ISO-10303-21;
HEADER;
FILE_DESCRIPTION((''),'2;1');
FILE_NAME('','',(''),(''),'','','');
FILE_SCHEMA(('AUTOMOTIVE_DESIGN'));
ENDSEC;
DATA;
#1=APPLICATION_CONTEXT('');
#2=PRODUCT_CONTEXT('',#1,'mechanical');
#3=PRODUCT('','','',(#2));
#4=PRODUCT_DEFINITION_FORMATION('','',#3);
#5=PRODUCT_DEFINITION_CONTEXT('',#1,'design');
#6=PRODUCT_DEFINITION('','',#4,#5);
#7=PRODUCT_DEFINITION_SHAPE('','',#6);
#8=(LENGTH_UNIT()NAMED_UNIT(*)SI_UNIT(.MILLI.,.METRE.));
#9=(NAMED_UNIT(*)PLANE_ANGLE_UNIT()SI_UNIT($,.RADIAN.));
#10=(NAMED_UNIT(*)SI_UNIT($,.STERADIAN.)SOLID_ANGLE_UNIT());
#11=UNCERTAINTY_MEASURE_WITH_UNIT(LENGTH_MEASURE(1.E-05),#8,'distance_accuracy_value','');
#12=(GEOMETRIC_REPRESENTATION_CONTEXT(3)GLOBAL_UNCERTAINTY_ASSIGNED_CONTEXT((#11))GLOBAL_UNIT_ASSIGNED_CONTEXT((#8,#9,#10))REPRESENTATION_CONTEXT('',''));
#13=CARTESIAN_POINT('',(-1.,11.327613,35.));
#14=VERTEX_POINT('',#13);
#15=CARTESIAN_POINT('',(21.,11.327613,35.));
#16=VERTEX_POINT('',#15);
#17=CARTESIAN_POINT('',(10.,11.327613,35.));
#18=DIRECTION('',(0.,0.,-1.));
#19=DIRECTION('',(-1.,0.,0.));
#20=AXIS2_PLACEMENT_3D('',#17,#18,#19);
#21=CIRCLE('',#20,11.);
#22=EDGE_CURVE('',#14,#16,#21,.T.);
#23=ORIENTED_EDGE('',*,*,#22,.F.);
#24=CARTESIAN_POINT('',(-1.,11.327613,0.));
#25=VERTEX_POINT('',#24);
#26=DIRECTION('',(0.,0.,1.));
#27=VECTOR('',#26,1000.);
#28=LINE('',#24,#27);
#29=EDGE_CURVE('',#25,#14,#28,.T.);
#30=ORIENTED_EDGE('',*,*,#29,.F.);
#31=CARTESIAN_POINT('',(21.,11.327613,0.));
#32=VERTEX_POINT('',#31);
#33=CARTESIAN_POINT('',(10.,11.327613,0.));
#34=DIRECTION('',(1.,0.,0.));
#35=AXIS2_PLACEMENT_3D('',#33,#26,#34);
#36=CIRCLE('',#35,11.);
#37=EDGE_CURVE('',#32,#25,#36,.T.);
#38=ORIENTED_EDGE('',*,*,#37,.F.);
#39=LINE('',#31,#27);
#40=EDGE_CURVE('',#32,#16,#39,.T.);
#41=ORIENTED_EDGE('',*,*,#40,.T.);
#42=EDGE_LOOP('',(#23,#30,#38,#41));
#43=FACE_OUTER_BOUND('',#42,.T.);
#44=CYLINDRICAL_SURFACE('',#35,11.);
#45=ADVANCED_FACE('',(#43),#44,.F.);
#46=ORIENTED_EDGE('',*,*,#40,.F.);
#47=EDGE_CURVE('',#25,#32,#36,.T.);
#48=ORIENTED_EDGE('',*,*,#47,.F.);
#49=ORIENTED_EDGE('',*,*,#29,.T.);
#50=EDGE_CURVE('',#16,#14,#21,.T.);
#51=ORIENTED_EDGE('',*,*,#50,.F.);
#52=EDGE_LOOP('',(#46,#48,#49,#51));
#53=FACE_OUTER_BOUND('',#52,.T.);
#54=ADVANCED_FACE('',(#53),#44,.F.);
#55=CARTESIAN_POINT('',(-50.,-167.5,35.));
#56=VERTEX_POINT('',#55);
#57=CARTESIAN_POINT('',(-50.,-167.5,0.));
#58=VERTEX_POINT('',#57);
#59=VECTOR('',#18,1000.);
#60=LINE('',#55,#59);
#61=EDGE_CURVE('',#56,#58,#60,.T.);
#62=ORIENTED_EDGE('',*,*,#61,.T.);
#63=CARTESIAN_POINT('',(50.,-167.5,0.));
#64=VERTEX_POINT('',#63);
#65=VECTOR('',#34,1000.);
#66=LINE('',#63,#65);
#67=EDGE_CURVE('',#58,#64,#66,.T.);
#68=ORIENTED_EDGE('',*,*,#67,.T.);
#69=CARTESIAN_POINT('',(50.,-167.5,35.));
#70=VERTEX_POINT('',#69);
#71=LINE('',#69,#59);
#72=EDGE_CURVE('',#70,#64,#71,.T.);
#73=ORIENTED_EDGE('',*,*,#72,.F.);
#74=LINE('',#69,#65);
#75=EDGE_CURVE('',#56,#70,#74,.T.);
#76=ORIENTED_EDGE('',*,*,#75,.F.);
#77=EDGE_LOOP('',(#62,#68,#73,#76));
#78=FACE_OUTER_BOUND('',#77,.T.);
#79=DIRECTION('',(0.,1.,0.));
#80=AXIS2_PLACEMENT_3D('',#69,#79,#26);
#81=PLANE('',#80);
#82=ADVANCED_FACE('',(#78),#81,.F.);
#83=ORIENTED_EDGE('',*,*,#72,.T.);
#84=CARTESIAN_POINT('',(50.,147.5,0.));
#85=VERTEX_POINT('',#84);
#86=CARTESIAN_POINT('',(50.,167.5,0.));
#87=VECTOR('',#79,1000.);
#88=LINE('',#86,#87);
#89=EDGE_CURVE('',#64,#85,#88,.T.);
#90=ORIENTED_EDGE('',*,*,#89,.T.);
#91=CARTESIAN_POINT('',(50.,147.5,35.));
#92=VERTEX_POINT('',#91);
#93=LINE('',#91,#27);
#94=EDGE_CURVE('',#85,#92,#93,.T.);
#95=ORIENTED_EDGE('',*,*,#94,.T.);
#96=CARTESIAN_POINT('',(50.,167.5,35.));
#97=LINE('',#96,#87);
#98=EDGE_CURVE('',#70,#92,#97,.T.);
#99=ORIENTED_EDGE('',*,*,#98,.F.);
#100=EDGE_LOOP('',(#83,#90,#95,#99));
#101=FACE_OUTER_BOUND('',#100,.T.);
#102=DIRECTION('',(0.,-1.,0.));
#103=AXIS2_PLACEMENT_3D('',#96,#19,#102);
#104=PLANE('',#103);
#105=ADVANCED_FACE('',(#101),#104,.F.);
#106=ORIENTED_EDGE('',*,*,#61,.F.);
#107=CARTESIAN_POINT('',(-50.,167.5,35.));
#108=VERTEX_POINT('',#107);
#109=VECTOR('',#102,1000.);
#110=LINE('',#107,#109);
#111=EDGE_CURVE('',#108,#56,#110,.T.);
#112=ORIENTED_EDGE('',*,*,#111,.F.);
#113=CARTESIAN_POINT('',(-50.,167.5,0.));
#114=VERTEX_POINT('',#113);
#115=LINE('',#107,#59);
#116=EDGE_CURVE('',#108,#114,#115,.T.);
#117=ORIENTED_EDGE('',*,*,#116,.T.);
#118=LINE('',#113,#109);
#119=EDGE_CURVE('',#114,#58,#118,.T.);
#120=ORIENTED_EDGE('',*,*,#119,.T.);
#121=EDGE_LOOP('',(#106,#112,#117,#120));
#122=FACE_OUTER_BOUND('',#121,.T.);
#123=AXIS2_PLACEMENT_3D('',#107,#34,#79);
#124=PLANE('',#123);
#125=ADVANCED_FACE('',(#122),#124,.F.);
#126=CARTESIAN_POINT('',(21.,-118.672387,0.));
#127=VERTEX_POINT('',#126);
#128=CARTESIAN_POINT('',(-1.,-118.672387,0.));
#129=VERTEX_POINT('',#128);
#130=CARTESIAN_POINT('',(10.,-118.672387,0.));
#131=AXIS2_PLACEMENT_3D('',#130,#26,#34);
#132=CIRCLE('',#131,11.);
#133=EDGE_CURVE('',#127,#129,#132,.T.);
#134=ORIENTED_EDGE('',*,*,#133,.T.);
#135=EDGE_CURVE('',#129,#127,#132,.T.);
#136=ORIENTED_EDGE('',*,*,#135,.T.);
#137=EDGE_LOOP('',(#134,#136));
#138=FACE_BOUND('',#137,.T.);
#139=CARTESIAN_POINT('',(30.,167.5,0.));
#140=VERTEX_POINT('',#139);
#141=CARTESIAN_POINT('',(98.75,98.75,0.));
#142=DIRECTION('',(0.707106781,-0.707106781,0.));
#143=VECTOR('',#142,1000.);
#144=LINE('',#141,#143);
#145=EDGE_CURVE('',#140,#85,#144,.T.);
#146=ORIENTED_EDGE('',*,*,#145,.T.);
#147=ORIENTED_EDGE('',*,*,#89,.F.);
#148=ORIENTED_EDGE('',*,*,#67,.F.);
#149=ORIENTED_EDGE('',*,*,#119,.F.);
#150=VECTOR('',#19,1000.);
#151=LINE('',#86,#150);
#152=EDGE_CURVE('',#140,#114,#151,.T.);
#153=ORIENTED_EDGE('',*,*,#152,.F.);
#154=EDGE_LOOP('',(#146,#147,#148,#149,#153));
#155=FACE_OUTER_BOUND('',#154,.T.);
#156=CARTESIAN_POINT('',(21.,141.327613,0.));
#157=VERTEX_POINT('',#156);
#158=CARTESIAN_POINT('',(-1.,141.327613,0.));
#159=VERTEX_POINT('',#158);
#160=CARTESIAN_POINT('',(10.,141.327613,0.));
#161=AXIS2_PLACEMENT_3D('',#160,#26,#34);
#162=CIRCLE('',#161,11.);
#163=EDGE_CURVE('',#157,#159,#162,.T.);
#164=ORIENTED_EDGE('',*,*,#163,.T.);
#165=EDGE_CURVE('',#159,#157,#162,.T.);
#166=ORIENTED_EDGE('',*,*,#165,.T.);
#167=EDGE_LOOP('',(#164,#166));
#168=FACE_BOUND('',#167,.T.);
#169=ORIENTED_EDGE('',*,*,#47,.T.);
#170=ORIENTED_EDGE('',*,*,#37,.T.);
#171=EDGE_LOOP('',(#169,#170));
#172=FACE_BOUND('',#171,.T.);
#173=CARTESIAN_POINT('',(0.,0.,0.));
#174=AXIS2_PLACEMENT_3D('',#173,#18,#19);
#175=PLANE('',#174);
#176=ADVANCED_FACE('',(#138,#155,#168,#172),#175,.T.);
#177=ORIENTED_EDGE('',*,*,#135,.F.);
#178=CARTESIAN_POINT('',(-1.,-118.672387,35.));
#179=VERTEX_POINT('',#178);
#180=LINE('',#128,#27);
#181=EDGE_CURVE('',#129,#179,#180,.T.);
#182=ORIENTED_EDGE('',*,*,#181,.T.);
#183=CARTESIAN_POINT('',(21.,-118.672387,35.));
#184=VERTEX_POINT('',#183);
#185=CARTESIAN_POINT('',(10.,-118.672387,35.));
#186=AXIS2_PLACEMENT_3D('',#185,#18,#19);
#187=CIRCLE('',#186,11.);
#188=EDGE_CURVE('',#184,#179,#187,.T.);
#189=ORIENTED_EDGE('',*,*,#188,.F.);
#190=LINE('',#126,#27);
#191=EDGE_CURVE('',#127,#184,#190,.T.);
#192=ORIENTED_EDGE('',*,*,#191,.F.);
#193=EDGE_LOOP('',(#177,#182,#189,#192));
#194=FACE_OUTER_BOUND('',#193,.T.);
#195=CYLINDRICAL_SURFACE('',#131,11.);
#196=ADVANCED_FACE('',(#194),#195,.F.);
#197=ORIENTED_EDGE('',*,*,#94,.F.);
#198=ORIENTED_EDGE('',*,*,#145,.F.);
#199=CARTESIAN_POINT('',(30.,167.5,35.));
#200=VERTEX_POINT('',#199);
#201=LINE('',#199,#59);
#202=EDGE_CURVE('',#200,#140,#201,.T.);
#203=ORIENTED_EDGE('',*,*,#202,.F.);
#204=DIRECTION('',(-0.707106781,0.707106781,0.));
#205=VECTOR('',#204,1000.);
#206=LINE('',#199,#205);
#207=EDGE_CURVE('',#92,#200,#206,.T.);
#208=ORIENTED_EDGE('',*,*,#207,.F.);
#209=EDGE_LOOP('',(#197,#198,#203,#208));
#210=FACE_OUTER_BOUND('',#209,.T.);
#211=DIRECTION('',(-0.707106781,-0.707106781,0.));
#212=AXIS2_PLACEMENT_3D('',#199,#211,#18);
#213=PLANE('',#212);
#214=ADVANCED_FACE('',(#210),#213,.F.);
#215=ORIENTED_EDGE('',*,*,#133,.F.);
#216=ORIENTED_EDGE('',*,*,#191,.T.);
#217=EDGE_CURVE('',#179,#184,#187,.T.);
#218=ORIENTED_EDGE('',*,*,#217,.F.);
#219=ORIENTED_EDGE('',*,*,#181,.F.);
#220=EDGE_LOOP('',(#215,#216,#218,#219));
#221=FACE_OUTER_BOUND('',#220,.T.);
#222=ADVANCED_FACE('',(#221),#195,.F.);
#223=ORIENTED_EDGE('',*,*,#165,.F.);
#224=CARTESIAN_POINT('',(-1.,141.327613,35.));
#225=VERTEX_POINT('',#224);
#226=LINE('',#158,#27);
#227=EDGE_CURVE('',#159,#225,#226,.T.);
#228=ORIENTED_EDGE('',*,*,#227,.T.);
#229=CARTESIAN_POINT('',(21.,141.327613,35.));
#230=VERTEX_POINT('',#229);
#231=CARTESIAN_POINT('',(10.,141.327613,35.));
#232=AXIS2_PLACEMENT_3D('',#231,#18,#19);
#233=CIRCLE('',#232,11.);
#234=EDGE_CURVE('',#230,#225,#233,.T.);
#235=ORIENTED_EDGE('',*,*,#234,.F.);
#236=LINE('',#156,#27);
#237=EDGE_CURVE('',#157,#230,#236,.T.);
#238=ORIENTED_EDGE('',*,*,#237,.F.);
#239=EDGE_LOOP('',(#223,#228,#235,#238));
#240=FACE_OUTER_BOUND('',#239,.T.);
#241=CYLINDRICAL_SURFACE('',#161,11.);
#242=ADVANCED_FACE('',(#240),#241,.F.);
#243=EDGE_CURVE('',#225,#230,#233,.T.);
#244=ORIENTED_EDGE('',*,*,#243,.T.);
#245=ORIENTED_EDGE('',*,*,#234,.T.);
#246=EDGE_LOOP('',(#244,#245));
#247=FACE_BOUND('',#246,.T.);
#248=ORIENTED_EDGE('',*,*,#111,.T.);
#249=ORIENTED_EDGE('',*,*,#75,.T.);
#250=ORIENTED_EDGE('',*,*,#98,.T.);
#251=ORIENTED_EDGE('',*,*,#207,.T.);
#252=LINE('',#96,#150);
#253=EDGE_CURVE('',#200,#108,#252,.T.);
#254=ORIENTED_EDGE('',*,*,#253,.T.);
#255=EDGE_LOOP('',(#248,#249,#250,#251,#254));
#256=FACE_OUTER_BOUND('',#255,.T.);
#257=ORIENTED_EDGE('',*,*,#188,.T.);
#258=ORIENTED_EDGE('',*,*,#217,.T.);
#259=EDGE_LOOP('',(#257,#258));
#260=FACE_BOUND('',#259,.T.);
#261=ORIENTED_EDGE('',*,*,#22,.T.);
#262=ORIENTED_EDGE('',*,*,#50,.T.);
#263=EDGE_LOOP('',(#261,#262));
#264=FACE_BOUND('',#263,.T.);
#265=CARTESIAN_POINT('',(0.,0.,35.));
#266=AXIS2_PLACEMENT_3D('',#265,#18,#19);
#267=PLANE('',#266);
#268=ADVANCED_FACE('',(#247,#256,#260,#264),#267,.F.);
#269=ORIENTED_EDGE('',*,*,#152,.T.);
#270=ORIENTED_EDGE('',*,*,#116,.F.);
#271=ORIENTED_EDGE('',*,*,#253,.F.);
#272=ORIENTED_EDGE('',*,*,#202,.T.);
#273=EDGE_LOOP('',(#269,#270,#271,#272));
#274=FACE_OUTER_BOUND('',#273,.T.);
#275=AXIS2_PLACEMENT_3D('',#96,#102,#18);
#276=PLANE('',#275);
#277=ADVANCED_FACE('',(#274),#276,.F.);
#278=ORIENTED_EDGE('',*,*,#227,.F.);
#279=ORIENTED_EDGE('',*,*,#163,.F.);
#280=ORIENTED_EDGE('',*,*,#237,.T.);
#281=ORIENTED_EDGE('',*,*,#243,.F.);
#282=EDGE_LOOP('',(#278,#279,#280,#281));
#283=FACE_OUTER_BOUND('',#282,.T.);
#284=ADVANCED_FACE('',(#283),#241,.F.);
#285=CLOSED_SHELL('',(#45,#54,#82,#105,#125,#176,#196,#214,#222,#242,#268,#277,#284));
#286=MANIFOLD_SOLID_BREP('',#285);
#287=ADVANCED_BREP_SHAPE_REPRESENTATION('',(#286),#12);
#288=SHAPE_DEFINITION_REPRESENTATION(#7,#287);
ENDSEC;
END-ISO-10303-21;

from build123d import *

# Parameters (mm, degrees)
SKETCH_1_W               = 100
SKETCH_1_H               = 335
EXTRUDE_1_DEPTH          = 35
CHAMFER_1_SIZE           = 20
CUT_EXTRUDE_1_DEPTH      = 179.27296486
CUT_EXTRUDE_1_DEPTH_BACK = 179.27296486
SKETCH_2_R               = 11


with BuildPart() as part:
    # 草图1 → 凸台-拉伸1 (new body)
    with BuildSketch(Plane.XY):
        Rectangle(SKETCH_1_W, SKETCH_1_H)
    extrude(amount=EXTRUDE_1_DEPTH)

    # 倒角1
    chamfer_1_edges = [part.edges().sort_by_distance(p)[0] for p in [
        (50, 167.5, 17.5),
    ]]
    chamfer(chamfer_1_edges, length=CHAMFER_1_SIZE)

    # 草图2 → 切除-拉伸1 (cut, two sides: drawn at the far end of the back side and taken through both)
    with BuildSketch(Plane.XY.offset(35).offset(-CUT_EXTRUDE_1_DEPTH_BACK)):
        with Locations((10, 141.327613457)):
            Circle(SKETCH_2_R)
        with Locations((10, -118.672386543)):
            Circle(SKETCH_2_R)
        with Locations((10, 11.327613457)):
            Circle(SKETCH_2_R)
    extrude(amount=CUT_EXTRUDE_1_DEPTH + CUT_EXTRUDE_1_DEPTH_BACK, mode=Mode.SUBTRACT)


solid = part.part
